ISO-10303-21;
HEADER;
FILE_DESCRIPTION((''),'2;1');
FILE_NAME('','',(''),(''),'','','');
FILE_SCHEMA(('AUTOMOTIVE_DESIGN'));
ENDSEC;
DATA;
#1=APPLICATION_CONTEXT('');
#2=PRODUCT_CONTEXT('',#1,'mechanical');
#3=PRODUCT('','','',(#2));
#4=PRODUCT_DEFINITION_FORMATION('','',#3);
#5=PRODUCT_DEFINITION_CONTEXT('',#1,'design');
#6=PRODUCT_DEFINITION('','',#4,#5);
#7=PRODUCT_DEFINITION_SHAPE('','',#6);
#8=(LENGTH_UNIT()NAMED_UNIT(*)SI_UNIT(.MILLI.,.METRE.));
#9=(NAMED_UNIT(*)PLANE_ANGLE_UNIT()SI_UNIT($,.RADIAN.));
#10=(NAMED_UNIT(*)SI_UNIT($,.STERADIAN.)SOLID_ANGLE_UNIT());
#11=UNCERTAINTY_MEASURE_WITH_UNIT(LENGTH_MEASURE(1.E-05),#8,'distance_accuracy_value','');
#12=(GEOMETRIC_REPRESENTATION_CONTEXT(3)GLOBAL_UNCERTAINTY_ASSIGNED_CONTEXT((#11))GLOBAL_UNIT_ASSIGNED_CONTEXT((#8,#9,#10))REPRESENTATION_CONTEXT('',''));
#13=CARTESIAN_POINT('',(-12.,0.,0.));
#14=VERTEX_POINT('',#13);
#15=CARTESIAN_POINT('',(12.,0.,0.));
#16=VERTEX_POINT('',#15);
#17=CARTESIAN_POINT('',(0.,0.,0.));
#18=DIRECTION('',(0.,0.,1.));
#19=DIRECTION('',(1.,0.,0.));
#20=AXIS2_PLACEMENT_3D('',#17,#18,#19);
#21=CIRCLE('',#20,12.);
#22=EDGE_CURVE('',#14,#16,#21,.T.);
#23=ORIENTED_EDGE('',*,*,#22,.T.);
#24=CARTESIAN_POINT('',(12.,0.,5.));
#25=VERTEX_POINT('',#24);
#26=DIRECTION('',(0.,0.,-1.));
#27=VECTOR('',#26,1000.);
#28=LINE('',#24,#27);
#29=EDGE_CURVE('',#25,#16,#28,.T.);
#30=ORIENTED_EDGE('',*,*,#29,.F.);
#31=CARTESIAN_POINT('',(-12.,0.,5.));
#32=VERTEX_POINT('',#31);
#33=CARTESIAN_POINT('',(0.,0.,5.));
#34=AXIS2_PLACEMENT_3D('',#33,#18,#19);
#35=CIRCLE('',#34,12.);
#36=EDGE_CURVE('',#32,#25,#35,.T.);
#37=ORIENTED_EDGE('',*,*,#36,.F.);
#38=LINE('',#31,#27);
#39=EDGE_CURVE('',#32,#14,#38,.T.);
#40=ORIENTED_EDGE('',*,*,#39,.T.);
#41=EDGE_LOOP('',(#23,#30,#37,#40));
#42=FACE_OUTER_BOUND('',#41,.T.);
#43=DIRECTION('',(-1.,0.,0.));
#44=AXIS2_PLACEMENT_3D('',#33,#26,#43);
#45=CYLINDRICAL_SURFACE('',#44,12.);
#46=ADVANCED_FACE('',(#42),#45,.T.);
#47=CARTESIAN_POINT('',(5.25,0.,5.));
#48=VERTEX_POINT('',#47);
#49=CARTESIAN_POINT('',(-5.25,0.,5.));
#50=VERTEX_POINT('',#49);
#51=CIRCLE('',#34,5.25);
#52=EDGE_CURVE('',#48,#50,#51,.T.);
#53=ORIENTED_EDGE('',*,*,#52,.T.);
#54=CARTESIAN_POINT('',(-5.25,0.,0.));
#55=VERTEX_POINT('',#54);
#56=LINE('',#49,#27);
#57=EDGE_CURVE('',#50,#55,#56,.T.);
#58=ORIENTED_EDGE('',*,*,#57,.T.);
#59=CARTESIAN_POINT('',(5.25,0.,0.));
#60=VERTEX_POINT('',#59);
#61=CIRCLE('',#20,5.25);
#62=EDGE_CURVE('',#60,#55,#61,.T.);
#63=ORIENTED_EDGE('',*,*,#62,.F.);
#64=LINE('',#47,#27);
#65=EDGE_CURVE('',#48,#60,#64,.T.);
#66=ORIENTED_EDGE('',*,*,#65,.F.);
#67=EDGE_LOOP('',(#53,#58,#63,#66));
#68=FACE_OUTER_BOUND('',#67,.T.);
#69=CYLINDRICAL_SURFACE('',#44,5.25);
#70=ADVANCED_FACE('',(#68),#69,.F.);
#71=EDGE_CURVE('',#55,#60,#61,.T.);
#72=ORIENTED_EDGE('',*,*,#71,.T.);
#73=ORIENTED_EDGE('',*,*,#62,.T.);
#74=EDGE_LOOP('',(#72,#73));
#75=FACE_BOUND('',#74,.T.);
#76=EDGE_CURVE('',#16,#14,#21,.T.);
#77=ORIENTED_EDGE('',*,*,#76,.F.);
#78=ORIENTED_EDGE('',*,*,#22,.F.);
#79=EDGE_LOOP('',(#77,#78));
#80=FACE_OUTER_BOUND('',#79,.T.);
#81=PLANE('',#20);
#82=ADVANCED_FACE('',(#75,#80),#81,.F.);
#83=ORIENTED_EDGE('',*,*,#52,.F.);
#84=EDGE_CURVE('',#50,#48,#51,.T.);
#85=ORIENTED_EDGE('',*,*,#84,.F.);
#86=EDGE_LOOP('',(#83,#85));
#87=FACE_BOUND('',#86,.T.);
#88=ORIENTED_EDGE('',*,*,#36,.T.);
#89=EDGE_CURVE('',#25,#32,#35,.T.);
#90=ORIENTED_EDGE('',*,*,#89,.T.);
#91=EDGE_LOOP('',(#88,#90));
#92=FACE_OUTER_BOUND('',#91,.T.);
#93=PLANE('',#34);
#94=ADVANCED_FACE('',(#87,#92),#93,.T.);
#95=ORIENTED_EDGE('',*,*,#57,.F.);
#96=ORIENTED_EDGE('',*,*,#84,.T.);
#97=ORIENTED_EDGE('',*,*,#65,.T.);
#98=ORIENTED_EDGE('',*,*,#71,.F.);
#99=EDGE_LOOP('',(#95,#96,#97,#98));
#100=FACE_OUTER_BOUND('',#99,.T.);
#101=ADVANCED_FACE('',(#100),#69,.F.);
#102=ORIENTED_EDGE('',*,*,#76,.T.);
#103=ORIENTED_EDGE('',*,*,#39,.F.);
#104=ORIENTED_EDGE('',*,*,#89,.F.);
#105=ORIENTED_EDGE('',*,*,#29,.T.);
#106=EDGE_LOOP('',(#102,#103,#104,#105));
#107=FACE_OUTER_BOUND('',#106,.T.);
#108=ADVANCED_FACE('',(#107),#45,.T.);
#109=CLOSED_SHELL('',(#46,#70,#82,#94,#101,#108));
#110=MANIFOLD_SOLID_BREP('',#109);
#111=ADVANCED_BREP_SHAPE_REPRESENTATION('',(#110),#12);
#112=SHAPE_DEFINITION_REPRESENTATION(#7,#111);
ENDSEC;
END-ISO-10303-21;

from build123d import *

# Parameters (mm, degrees)
SKETCH1_R           = 12
SKETCH1_R_2         = 5.25
BOSS_EXTRUDE1_DEPTH = 5


with BuildPart() as part:
    # Sketch1 → Boss-Extrude1 (new body)
    with BuildSketch(Plane.XY):
        Circle(SKETCH1_R)
        Circle(SKETCH1_R_2, mode=Mode.SUBTRACT)
    extrude(amount=BOSS_EXTRUDE1_DEPTH)


solid = part.part
